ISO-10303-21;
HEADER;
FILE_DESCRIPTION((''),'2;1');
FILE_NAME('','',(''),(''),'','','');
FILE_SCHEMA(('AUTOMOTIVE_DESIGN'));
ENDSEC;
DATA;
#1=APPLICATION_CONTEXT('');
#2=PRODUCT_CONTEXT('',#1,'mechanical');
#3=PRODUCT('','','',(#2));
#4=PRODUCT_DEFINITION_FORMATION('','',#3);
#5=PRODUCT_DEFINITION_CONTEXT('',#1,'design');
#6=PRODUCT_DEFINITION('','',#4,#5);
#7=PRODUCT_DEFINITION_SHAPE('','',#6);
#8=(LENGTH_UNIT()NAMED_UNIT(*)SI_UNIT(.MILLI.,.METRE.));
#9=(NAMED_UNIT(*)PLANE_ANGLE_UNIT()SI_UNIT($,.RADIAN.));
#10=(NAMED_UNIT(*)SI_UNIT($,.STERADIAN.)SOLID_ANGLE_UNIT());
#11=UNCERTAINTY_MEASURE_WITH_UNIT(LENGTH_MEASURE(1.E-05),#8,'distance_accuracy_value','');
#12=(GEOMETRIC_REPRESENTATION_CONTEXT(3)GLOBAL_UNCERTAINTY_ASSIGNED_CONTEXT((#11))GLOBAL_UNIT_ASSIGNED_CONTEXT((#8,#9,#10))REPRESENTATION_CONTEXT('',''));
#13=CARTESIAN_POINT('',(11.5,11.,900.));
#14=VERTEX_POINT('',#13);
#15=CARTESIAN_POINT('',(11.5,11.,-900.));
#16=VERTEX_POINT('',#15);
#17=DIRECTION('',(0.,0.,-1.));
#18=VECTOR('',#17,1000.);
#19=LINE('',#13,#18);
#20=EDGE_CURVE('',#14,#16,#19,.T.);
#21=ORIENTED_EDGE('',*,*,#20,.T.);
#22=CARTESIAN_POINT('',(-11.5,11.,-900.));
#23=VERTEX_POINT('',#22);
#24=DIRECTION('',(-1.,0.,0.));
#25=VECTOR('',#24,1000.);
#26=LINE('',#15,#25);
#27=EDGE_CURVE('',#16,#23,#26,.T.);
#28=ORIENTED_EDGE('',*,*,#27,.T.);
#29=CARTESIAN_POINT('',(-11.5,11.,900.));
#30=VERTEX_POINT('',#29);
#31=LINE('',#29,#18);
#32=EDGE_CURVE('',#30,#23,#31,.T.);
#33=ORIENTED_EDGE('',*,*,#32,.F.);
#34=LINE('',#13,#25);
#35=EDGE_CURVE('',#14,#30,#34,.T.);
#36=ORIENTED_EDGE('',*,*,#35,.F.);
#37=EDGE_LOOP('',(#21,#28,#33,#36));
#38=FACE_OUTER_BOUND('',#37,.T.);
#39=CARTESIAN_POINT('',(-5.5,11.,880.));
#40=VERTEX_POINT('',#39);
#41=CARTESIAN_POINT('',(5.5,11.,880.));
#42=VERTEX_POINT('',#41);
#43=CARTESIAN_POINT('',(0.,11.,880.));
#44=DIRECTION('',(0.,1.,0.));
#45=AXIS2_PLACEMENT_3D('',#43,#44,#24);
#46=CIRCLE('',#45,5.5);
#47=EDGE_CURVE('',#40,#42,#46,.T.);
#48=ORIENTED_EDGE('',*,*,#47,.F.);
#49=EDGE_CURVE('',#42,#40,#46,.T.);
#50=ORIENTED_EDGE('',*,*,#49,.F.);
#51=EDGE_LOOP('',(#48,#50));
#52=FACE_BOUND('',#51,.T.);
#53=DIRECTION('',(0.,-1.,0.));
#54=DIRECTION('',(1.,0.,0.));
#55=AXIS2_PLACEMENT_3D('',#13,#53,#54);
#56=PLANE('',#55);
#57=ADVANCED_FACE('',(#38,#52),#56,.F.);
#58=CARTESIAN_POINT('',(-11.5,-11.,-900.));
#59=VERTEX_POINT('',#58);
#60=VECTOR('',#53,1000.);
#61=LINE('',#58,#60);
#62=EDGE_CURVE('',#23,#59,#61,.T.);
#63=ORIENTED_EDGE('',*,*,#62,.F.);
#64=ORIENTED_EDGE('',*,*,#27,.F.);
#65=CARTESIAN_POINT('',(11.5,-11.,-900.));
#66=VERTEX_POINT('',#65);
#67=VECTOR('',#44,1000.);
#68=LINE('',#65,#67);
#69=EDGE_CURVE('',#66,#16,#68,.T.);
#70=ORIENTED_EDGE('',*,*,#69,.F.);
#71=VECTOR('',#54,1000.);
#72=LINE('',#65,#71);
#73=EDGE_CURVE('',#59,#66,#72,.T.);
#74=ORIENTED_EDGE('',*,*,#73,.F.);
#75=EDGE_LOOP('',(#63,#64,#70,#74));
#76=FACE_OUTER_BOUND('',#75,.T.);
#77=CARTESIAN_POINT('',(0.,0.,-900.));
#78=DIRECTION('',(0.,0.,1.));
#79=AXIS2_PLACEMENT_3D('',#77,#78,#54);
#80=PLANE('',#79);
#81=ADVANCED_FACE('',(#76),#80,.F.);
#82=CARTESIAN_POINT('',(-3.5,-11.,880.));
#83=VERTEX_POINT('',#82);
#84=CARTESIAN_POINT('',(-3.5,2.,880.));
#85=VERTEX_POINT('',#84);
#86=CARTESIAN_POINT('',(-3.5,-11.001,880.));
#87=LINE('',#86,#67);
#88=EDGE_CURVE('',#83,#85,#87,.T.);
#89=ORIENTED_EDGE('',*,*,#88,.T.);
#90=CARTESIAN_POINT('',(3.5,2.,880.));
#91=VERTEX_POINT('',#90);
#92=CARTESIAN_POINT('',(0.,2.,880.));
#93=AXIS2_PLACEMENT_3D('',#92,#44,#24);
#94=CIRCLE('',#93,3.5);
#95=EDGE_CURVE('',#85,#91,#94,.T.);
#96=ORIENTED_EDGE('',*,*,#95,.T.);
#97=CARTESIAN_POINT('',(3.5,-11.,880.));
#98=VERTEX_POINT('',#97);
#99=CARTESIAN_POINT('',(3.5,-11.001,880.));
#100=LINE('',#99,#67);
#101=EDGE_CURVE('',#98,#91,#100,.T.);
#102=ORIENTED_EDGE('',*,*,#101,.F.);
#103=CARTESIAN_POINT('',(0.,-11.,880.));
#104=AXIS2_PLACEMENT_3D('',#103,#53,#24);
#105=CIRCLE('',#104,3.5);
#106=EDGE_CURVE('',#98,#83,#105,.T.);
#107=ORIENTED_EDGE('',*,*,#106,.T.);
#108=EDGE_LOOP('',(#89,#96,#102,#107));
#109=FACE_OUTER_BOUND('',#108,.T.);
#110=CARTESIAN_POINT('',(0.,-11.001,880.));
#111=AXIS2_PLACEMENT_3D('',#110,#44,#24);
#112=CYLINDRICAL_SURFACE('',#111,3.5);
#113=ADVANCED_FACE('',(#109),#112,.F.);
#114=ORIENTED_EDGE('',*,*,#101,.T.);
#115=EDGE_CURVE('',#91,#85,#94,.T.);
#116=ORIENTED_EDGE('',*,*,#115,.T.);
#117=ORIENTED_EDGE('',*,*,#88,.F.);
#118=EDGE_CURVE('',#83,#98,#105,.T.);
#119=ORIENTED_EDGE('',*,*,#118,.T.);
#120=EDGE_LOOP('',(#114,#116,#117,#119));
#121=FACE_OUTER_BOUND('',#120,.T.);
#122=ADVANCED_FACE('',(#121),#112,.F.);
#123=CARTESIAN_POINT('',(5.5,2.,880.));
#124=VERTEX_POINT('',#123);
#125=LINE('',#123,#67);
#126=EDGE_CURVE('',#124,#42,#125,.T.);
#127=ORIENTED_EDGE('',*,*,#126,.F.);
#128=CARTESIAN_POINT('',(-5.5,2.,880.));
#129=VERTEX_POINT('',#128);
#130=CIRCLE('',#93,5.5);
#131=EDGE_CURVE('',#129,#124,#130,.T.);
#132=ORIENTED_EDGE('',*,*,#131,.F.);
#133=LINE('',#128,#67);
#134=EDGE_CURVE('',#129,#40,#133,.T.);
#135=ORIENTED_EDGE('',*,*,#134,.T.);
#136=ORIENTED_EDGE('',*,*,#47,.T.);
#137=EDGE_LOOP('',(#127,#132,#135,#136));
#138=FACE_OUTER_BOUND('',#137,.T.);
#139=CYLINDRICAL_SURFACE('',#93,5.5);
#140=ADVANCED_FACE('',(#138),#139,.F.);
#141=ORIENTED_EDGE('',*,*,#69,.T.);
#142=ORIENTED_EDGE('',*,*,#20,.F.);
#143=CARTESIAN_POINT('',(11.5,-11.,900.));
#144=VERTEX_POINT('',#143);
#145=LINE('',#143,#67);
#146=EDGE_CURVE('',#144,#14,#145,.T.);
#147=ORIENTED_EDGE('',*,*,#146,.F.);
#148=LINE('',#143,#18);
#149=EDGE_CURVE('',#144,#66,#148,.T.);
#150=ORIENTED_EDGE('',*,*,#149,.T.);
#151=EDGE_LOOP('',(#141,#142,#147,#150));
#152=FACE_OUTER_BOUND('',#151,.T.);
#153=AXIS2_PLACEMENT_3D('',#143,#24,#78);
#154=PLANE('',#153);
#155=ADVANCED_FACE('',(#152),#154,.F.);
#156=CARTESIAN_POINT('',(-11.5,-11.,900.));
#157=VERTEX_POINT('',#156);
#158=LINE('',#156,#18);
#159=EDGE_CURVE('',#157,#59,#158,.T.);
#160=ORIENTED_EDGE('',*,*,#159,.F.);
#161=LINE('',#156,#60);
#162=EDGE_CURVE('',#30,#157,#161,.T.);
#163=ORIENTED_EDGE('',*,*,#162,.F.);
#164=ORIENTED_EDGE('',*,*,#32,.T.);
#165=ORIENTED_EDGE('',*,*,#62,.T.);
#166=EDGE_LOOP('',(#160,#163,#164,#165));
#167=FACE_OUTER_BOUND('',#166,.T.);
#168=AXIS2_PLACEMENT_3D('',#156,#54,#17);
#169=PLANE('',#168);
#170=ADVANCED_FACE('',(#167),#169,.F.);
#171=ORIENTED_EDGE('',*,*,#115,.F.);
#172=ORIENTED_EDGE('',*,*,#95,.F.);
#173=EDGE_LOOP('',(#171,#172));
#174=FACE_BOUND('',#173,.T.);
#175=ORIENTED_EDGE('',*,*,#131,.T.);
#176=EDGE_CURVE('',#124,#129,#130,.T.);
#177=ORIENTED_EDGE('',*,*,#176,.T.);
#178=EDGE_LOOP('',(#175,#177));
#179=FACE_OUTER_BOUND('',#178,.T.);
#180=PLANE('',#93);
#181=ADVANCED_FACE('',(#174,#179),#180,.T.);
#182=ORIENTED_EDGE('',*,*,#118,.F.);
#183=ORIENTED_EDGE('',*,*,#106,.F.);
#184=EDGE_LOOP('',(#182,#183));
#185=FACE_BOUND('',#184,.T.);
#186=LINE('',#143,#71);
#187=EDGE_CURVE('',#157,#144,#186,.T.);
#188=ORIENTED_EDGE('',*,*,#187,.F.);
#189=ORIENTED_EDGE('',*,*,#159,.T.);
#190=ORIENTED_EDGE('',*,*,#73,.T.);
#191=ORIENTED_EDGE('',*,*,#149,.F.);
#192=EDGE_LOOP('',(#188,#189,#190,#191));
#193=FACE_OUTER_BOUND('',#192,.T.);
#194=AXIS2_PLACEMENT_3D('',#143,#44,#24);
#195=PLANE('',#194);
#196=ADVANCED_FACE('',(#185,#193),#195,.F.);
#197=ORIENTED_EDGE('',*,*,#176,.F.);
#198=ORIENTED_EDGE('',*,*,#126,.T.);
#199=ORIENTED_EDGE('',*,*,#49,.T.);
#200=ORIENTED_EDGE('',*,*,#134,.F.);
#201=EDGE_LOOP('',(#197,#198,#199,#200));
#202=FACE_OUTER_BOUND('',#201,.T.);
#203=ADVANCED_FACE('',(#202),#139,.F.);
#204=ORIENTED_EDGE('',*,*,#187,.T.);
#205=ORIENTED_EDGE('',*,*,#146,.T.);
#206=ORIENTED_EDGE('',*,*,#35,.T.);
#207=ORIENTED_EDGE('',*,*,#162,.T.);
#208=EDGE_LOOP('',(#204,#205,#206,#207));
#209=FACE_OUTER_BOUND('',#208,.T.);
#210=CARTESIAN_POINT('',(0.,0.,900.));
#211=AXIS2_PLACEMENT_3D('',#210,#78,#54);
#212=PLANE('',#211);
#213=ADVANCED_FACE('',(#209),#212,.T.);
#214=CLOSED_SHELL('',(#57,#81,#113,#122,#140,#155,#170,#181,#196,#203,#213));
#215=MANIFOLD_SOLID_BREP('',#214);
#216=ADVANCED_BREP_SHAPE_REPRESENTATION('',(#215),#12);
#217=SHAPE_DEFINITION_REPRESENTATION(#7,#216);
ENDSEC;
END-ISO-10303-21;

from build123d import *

# Parameters (mm, degrees)
SKETCH_1_W          = 23
SKETCH_1_H          = 22
EXTRUDE_1_DEPTH     = 900
SKETCH_2_R          = 5.5
CUT_EXTRUDE_1_DEPTH = 9
CUT_EXTRUDE_2_REACH = 902.167
SKETCH_3_R          = 3.5


with BuildPart() as part:
    # 草图1 → 凸台-拉伸1 (new, symmetric)
    with BuildSketch(Plane.XY):
        Rectangle(SKETCH_1_W, SKETCH_1_H)
    extrude(amount=EXTRUDE_1_DEPTH, both=True)

    # 草图2 → 切除-拉伸1 (cut)
    with BuildSketch(Plane(origin=(0, 11, 0), x_dir=(1, 0, 0), z_dir=(0, 1, 0))):
        with Locations(Location((0, -880, 0), (0, 0, 180))):
            Circle(SKETCH_2_R)
    extrude(amount=-CUT_EXTRUDE_1_DEPTH, mode=Mode.SUBTRACT)

    # 草图3 → 切除-拉伸2 (cut, up to next)
    with BuildSketch(Plane(origin=(0, 2, 0), x_dir=(1, 0, 0), z_dir=(0, 1, 0)), mode=Mode.PRIVATE) as cut_extrude_2_sk1:
        with Locations(Location((0, -880, 0), (0, 0, 180))):
            Circle(SKETCH_3_R)
    cut_extrude_2_tool1 = extrude(cut_extrude_2_sk1.sketch, amount=-CUT_EXTRUDE_2_REACH, mode=Mode.PRIVATE) & part.part
    add(cut_extrude_2_tool1.solids().sort_by_distance((0, 2, 880))[0], mode=Mode.SUBTRACT)


solid = part.part
